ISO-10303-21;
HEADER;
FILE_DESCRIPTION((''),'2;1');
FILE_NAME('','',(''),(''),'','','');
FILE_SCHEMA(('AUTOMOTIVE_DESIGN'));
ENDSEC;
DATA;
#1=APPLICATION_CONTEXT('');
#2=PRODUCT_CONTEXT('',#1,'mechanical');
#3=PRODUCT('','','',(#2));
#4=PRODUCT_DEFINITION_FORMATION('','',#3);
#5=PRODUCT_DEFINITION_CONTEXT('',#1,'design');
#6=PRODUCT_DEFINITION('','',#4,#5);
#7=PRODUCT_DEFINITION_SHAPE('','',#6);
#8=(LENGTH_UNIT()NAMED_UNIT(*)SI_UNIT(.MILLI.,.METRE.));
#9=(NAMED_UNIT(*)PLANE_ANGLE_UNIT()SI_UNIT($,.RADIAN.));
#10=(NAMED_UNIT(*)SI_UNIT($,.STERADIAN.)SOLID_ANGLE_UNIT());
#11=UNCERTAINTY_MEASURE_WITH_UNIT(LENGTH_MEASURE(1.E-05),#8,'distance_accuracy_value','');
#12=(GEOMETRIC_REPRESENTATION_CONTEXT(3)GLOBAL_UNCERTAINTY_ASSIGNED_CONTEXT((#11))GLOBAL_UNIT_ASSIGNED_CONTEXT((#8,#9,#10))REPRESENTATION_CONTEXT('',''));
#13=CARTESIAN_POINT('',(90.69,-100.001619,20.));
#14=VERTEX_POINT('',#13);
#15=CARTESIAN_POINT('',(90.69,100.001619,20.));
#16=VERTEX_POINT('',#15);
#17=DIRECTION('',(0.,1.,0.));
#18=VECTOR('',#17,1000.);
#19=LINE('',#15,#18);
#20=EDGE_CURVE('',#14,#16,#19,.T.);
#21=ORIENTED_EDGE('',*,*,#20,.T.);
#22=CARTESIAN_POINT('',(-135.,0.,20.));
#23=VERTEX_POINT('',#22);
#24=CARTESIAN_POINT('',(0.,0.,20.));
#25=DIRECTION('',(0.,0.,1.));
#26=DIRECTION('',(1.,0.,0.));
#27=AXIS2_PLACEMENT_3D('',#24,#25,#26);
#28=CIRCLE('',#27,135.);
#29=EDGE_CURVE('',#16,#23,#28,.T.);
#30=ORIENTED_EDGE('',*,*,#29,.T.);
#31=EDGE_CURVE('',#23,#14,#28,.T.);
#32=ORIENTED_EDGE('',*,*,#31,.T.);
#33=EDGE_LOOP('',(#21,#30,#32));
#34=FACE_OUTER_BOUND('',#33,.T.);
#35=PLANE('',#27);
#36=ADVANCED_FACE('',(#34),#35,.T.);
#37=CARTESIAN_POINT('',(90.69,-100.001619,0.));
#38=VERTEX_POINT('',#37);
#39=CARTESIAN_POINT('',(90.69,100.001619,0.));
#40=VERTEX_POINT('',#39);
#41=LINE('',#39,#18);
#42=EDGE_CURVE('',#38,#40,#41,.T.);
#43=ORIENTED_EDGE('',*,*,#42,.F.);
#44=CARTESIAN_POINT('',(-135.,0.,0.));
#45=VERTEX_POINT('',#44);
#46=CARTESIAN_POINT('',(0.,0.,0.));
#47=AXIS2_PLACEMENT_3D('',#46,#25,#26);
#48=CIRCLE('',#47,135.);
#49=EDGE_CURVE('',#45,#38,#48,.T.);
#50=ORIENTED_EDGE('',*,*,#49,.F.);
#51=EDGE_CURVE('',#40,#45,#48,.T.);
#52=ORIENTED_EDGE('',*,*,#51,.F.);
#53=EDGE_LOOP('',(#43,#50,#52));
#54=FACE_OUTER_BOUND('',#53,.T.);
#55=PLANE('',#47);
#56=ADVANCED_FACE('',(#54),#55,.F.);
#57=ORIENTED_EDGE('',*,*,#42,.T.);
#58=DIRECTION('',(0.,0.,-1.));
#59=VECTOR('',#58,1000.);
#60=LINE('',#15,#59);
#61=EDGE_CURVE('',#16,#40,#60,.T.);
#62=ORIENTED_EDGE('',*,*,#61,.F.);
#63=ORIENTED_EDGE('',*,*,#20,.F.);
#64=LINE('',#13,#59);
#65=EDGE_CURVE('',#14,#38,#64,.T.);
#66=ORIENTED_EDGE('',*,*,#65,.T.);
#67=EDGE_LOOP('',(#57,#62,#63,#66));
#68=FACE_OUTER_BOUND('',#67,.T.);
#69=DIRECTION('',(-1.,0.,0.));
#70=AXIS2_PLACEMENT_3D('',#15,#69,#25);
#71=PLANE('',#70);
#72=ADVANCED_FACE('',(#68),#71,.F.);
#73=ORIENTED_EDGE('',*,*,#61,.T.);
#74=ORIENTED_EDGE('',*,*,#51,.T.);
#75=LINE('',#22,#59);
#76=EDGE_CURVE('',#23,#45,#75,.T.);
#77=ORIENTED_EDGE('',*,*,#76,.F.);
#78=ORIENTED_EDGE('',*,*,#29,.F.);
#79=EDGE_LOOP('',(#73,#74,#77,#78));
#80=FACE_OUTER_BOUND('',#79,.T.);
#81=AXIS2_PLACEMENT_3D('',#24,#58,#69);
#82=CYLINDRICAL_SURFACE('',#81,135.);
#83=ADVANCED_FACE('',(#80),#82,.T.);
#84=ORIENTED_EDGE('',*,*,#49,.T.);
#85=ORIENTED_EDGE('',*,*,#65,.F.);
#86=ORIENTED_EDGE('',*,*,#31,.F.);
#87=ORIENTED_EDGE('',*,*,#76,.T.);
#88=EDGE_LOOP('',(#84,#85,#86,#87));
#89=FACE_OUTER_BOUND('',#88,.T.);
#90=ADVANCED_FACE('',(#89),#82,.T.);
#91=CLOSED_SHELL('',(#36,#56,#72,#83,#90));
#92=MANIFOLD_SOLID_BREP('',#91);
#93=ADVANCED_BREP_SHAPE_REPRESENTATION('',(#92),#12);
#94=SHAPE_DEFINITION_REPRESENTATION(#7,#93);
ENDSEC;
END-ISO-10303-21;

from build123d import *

# Parameters (mm, degrees)
BOSS_EXTRUDE1_DEPTH = 20


with BuildPart() as part:
    # Sketch1 → Boss-Extrude1 (new body)
    with BuildSketch(Plane.XY):
        with BuildLine():
            Line((90.69, 100.001619487), (90.69, -100.001619487))
            ThreePointArc((90.69, -100.001619487), (-135, 0), (90.69, 100.001619487))
        make_face()
    extrude(amount=BOSS_EXTRUDE1_DEPTH)


solid = part.part
